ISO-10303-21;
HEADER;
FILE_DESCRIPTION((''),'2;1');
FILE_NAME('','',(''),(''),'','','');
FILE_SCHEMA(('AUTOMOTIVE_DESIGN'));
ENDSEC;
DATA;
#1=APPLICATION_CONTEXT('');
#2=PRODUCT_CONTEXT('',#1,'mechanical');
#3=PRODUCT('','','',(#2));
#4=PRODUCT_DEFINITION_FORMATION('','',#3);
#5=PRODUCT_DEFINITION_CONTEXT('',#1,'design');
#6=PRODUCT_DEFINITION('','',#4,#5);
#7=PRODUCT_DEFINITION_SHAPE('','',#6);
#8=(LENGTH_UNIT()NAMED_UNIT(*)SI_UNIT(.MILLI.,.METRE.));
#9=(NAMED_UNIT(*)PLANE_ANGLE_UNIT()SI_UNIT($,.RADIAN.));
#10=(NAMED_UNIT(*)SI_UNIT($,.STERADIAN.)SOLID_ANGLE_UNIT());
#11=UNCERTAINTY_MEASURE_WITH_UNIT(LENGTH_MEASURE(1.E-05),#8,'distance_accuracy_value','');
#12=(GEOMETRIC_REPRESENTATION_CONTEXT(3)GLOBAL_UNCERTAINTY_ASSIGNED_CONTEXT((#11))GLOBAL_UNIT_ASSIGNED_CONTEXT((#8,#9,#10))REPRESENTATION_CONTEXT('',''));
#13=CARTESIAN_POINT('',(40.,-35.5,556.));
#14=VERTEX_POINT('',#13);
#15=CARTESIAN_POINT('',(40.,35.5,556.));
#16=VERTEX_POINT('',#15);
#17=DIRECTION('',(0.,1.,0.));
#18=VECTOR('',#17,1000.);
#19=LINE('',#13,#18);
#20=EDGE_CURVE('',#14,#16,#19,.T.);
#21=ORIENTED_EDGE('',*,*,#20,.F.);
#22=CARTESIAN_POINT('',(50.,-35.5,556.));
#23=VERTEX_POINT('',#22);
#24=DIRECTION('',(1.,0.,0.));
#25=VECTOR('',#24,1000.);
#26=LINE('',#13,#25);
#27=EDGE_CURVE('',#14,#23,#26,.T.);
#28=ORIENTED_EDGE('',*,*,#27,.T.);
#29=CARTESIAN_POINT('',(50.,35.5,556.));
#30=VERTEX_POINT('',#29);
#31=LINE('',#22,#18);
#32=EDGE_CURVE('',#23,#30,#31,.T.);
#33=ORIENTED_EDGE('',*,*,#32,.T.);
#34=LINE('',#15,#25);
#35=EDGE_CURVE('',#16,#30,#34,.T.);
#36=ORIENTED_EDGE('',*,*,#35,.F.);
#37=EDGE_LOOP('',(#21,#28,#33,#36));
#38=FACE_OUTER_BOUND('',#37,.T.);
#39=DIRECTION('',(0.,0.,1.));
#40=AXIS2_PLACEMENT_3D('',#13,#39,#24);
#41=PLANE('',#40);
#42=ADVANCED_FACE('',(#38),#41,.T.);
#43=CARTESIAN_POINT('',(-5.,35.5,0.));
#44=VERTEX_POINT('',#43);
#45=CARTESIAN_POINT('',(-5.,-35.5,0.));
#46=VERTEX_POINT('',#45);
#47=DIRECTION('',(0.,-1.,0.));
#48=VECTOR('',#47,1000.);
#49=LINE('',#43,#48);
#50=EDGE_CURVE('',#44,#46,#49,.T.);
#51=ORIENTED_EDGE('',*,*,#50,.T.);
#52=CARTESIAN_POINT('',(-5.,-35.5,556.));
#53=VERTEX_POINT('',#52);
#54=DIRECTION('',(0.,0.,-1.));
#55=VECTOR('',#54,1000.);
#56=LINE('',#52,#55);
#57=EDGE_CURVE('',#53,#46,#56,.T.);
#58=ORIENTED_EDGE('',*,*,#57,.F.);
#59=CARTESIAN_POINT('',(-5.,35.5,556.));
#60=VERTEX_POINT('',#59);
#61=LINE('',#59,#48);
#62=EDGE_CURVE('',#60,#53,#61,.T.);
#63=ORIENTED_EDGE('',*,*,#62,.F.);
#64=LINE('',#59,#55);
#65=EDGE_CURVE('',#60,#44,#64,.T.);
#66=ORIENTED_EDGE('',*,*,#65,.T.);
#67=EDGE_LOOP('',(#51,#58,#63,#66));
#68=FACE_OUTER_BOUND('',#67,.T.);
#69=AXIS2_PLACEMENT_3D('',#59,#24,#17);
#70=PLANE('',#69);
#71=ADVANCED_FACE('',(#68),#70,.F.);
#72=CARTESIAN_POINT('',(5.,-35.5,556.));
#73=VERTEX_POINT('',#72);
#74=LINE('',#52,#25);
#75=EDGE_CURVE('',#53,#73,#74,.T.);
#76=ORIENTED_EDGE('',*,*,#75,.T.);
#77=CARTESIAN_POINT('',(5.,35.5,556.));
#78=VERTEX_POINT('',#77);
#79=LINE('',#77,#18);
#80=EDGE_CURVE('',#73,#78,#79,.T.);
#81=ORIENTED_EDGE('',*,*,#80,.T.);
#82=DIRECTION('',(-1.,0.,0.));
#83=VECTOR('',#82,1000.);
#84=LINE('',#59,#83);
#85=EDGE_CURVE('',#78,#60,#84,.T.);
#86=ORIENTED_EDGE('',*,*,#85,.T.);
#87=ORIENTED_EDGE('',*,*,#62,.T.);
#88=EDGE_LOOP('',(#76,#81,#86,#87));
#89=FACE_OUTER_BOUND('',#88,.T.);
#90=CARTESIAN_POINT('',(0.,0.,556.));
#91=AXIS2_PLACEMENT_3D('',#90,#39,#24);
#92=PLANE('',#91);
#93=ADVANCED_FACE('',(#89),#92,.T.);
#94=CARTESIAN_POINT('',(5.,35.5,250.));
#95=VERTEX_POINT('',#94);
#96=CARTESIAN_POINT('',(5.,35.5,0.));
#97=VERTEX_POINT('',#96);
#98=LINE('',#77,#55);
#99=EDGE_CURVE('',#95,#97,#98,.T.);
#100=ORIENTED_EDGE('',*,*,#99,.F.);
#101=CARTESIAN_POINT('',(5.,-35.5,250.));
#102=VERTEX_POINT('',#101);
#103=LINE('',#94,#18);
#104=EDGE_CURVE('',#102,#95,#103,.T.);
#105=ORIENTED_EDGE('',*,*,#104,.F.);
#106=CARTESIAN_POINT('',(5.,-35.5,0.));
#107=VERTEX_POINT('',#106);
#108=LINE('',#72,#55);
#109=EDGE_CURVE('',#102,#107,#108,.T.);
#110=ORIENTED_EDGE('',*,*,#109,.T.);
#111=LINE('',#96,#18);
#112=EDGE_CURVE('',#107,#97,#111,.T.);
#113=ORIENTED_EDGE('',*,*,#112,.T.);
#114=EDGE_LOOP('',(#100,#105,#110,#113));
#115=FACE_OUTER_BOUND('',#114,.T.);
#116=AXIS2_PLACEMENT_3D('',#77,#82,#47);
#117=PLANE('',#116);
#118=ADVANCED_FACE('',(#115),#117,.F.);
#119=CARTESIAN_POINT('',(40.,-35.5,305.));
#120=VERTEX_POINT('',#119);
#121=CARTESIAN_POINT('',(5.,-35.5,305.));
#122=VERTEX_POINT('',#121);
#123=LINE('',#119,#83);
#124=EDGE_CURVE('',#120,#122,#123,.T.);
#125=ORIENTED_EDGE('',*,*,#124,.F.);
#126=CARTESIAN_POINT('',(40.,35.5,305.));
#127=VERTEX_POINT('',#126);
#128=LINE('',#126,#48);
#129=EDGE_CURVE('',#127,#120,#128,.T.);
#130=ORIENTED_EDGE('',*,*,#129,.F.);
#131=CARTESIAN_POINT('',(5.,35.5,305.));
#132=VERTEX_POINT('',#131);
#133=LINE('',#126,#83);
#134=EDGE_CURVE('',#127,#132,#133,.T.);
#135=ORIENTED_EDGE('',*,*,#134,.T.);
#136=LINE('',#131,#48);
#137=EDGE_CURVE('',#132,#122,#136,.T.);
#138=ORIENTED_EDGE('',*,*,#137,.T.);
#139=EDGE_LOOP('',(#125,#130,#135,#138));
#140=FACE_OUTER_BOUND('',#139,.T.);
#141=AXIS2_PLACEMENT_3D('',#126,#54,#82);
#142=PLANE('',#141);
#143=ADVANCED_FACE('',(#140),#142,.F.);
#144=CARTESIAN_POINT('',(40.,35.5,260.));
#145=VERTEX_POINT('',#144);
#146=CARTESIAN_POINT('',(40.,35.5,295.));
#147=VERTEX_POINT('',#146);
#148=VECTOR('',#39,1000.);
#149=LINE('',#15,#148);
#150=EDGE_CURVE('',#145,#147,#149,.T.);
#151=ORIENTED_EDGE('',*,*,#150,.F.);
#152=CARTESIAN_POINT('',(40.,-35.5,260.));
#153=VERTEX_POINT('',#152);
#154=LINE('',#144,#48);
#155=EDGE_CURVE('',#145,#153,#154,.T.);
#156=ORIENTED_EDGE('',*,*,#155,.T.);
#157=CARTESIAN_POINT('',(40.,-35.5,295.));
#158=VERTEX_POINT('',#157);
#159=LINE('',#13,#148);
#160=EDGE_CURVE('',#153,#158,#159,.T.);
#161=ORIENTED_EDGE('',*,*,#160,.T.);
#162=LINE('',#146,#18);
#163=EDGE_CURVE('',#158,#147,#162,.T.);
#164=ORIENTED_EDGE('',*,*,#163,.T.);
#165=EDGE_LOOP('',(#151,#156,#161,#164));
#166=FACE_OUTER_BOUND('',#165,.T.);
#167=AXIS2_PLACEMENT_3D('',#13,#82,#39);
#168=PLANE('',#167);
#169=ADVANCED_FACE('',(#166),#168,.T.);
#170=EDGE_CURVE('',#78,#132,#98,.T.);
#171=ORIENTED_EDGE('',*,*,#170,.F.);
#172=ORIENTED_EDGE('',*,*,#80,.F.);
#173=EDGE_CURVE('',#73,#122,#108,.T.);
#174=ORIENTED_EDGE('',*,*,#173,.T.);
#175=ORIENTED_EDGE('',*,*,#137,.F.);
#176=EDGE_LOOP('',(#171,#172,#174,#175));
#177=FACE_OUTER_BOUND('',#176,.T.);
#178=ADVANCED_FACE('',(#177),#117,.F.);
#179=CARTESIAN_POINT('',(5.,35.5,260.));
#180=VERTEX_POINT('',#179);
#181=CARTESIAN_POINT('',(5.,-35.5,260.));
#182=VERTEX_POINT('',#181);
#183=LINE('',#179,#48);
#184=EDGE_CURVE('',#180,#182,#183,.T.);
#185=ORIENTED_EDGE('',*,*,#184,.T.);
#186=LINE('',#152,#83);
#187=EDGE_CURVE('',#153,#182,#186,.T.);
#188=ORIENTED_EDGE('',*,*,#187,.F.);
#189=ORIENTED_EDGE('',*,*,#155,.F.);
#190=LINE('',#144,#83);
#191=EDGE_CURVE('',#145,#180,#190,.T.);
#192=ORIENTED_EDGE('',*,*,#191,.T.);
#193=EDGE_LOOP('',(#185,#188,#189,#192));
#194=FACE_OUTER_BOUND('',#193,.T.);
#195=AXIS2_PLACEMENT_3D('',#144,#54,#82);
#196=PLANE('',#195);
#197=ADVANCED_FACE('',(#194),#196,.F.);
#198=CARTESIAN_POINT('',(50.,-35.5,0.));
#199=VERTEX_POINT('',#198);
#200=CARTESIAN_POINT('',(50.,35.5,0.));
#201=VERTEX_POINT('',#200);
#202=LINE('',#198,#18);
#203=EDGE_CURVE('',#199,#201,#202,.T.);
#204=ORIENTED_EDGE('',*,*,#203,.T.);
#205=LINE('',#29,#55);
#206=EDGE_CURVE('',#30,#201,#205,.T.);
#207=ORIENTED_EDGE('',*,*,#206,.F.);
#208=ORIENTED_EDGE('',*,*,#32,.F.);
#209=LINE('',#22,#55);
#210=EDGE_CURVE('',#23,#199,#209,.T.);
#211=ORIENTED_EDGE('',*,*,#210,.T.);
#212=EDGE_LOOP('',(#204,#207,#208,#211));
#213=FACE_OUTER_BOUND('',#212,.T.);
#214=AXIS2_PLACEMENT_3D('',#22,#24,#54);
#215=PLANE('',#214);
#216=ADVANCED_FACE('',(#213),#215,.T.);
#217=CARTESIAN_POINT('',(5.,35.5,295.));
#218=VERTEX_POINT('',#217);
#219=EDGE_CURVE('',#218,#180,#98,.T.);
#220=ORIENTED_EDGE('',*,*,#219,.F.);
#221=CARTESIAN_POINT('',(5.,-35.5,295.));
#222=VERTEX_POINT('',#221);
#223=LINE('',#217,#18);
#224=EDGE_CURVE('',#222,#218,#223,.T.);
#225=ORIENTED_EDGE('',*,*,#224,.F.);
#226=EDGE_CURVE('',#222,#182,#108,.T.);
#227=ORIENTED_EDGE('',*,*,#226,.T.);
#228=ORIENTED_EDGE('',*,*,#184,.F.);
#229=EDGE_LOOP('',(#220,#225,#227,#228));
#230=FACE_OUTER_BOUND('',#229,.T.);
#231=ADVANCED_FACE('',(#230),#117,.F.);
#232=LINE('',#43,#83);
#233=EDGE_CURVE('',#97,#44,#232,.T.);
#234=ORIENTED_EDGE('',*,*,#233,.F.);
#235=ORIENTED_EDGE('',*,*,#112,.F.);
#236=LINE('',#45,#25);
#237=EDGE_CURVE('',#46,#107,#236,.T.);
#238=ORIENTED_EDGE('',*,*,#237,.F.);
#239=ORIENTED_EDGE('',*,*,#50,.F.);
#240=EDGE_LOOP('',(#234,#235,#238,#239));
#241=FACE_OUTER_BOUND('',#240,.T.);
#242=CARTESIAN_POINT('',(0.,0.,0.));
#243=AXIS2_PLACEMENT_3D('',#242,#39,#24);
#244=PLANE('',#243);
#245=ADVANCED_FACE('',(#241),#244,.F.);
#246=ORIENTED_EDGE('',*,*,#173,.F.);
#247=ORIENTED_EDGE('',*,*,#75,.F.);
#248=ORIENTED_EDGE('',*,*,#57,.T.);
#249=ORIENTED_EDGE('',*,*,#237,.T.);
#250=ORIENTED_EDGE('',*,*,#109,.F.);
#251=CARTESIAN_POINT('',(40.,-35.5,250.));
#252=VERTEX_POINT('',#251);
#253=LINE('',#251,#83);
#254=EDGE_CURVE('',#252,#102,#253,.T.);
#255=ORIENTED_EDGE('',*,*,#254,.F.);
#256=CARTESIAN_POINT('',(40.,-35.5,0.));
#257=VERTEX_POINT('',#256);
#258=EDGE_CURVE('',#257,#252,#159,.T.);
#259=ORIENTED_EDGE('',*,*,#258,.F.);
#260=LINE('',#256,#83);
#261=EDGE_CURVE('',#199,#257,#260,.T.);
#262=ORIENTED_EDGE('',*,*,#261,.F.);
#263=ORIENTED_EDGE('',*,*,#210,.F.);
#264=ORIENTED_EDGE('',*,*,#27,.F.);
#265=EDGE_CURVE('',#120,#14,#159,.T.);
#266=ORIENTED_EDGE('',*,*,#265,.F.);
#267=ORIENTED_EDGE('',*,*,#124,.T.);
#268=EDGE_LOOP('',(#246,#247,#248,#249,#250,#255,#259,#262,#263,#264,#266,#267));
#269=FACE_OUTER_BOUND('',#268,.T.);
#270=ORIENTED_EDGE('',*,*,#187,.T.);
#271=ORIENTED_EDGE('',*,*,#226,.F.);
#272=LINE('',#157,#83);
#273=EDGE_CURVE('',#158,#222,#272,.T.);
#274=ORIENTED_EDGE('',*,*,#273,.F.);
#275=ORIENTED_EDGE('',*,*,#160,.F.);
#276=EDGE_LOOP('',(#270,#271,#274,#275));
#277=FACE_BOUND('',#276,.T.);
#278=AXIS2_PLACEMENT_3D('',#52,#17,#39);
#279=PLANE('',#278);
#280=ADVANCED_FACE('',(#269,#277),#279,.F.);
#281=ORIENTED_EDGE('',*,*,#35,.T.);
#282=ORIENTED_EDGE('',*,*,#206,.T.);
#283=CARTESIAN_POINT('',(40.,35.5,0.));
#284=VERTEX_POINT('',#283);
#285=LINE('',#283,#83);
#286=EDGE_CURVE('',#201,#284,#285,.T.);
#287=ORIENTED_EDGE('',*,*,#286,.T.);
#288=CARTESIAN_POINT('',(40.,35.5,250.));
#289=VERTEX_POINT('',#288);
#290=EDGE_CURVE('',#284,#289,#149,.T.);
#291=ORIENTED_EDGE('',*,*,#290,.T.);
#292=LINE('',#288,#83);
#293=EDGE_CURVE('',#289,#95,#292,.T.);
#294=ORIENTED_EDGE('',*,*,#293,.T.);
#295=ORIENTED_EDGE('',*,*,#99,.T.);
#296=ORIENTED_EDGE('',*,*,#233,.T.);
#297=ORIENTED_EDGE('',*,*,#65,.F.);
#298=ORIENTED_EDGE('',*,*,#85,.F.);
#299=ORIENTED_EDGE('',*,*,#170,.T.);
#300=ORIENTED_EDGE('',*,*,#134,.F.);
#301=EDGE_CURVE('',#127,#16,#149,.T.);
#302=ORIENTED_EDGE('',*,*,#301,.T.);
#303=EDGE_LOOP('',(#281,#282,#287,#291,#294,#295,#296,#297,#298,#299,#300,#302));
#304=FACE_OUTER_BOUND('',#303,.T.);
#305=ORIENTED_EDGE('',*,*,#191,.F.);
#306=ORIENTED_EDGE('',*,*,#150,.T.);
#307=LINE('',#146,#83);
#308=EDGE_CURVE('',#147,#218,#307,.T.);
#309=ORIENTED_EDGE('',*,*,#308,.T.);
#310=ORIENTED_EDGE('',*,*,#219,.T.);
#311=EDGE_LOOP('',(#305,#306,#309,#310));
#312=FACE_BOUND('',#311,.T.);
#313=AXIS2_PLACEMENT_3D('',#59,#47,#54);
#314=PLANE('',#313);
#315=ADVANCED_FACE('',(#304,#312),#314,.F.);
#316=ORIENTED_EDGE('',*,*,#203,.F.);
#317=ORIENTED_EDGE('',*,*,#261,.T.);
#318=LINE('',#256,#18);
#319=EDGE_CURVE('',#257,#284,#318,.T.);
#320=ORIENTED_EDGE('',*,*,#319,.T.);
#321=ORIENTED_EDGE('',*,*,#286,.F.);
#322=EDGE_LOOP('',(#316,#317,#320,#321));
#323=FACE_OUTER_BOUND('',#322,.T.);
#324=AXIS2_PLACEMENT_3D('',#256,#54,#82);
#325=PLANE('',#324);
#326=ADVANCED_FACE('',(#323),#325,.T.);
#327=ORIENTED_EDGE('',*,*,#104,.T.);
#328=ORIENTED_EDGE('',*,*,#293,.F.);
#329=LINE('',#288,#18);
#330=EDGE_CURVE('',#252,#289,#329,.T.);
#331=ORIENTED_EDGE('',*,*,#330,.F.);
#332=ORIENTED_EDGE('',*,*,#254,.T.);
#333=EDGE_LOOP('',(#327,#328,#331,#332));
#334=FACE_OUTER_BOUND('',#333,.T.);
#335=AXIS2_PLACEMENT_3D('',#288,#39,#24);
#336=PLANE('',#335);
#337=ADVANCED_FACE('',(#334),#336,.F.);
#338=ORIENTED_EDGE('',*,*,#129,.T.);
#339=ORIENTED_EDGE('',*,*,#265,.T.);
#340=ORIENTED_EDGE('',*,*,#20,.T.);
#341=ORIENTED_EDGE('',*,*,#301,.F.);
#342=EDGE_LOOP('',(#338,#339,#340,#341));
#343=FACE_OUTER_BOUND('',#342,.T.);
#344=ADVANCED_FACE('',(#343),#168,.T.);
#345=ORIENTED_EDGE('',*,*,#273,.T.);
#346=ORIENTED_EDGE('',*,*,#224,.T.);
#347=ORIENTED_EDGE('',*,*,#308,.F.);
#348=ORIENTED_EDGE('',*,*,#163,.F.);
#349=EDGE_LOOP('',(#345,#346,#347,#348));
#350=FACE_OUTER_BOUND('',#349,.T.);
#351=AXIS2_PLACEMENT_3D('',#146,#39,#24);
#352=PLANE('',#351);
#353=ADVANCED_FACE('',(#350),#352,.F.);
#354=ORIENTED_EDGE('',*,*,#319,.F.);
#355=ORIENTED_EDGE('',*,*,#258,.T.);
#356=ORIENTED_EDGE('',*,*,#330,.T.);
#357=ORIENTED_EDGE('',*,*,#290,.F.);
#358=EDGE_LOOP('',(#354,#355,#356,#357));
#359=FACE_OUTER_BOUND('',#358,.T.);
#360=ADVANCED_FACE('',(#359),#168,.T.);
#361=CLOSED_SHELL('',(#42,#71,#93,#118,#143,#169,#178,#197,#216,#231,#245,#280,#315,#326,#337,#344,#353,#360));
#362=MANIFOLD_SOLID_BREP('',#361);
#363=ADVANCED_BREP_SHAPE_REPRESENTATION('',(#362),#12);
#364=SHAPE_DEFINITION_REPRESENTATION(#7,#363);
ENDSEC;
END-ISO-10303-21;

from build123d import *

# Parameters (mm, degrees)
SKETCH1_W           = 10
SKETCH1_H           = 71
BOSS_EXTRUDE1_DEPTH = 556
SKETCH2_W           = 10
SKETCH2_H           = 71
BOSS_EXTRUDE2_DEPTH = 35
SKETCH3_W           = 10
SKETCH3_H           = 556
BOSS_EXTRUDE3_DEPTH = 71


with BuildPart() as part:
    # Sketch1 → Boss-Extrude1 (new body)
    with BuildSketch(Plane.XY):
        Rectangle(SKETCH1_W, SKETCH1_H)
    extrude(amount=BOSS_EXTRUDE1_DEPTH)

    # Sketch2 → Boss-Extrude2 (add)
    with BuildSketch(Plane(origin=(5, 0, 0), x_dir=(0, 0, -1), z_dir=(1, 0, 0))):
        with Locations((-300, 0)):
            Rectangle(SKETCH2_W, SKETCH2_H)
        with Locations((-255, 0)):
            Rectangle(SKETCH2_W, SKETCH2_H)
    extrude(amount=BOSS_EXTRUDE2_DEPTH)

    # Sketch3 → Boss-Extrude3 (add)
    with BuildSketch(Plane(origin=(0, 35.5, 0), x_dir=(1, 0, 0), z_dir=(0, 1, 0))):
        with Locations((45, -278)):
            Rectangle(SKETCH3_W, SKETCH3_H)
    extrude(amount=-BOSS_EXTRUDE3_DEPTH)


solid = part.part
